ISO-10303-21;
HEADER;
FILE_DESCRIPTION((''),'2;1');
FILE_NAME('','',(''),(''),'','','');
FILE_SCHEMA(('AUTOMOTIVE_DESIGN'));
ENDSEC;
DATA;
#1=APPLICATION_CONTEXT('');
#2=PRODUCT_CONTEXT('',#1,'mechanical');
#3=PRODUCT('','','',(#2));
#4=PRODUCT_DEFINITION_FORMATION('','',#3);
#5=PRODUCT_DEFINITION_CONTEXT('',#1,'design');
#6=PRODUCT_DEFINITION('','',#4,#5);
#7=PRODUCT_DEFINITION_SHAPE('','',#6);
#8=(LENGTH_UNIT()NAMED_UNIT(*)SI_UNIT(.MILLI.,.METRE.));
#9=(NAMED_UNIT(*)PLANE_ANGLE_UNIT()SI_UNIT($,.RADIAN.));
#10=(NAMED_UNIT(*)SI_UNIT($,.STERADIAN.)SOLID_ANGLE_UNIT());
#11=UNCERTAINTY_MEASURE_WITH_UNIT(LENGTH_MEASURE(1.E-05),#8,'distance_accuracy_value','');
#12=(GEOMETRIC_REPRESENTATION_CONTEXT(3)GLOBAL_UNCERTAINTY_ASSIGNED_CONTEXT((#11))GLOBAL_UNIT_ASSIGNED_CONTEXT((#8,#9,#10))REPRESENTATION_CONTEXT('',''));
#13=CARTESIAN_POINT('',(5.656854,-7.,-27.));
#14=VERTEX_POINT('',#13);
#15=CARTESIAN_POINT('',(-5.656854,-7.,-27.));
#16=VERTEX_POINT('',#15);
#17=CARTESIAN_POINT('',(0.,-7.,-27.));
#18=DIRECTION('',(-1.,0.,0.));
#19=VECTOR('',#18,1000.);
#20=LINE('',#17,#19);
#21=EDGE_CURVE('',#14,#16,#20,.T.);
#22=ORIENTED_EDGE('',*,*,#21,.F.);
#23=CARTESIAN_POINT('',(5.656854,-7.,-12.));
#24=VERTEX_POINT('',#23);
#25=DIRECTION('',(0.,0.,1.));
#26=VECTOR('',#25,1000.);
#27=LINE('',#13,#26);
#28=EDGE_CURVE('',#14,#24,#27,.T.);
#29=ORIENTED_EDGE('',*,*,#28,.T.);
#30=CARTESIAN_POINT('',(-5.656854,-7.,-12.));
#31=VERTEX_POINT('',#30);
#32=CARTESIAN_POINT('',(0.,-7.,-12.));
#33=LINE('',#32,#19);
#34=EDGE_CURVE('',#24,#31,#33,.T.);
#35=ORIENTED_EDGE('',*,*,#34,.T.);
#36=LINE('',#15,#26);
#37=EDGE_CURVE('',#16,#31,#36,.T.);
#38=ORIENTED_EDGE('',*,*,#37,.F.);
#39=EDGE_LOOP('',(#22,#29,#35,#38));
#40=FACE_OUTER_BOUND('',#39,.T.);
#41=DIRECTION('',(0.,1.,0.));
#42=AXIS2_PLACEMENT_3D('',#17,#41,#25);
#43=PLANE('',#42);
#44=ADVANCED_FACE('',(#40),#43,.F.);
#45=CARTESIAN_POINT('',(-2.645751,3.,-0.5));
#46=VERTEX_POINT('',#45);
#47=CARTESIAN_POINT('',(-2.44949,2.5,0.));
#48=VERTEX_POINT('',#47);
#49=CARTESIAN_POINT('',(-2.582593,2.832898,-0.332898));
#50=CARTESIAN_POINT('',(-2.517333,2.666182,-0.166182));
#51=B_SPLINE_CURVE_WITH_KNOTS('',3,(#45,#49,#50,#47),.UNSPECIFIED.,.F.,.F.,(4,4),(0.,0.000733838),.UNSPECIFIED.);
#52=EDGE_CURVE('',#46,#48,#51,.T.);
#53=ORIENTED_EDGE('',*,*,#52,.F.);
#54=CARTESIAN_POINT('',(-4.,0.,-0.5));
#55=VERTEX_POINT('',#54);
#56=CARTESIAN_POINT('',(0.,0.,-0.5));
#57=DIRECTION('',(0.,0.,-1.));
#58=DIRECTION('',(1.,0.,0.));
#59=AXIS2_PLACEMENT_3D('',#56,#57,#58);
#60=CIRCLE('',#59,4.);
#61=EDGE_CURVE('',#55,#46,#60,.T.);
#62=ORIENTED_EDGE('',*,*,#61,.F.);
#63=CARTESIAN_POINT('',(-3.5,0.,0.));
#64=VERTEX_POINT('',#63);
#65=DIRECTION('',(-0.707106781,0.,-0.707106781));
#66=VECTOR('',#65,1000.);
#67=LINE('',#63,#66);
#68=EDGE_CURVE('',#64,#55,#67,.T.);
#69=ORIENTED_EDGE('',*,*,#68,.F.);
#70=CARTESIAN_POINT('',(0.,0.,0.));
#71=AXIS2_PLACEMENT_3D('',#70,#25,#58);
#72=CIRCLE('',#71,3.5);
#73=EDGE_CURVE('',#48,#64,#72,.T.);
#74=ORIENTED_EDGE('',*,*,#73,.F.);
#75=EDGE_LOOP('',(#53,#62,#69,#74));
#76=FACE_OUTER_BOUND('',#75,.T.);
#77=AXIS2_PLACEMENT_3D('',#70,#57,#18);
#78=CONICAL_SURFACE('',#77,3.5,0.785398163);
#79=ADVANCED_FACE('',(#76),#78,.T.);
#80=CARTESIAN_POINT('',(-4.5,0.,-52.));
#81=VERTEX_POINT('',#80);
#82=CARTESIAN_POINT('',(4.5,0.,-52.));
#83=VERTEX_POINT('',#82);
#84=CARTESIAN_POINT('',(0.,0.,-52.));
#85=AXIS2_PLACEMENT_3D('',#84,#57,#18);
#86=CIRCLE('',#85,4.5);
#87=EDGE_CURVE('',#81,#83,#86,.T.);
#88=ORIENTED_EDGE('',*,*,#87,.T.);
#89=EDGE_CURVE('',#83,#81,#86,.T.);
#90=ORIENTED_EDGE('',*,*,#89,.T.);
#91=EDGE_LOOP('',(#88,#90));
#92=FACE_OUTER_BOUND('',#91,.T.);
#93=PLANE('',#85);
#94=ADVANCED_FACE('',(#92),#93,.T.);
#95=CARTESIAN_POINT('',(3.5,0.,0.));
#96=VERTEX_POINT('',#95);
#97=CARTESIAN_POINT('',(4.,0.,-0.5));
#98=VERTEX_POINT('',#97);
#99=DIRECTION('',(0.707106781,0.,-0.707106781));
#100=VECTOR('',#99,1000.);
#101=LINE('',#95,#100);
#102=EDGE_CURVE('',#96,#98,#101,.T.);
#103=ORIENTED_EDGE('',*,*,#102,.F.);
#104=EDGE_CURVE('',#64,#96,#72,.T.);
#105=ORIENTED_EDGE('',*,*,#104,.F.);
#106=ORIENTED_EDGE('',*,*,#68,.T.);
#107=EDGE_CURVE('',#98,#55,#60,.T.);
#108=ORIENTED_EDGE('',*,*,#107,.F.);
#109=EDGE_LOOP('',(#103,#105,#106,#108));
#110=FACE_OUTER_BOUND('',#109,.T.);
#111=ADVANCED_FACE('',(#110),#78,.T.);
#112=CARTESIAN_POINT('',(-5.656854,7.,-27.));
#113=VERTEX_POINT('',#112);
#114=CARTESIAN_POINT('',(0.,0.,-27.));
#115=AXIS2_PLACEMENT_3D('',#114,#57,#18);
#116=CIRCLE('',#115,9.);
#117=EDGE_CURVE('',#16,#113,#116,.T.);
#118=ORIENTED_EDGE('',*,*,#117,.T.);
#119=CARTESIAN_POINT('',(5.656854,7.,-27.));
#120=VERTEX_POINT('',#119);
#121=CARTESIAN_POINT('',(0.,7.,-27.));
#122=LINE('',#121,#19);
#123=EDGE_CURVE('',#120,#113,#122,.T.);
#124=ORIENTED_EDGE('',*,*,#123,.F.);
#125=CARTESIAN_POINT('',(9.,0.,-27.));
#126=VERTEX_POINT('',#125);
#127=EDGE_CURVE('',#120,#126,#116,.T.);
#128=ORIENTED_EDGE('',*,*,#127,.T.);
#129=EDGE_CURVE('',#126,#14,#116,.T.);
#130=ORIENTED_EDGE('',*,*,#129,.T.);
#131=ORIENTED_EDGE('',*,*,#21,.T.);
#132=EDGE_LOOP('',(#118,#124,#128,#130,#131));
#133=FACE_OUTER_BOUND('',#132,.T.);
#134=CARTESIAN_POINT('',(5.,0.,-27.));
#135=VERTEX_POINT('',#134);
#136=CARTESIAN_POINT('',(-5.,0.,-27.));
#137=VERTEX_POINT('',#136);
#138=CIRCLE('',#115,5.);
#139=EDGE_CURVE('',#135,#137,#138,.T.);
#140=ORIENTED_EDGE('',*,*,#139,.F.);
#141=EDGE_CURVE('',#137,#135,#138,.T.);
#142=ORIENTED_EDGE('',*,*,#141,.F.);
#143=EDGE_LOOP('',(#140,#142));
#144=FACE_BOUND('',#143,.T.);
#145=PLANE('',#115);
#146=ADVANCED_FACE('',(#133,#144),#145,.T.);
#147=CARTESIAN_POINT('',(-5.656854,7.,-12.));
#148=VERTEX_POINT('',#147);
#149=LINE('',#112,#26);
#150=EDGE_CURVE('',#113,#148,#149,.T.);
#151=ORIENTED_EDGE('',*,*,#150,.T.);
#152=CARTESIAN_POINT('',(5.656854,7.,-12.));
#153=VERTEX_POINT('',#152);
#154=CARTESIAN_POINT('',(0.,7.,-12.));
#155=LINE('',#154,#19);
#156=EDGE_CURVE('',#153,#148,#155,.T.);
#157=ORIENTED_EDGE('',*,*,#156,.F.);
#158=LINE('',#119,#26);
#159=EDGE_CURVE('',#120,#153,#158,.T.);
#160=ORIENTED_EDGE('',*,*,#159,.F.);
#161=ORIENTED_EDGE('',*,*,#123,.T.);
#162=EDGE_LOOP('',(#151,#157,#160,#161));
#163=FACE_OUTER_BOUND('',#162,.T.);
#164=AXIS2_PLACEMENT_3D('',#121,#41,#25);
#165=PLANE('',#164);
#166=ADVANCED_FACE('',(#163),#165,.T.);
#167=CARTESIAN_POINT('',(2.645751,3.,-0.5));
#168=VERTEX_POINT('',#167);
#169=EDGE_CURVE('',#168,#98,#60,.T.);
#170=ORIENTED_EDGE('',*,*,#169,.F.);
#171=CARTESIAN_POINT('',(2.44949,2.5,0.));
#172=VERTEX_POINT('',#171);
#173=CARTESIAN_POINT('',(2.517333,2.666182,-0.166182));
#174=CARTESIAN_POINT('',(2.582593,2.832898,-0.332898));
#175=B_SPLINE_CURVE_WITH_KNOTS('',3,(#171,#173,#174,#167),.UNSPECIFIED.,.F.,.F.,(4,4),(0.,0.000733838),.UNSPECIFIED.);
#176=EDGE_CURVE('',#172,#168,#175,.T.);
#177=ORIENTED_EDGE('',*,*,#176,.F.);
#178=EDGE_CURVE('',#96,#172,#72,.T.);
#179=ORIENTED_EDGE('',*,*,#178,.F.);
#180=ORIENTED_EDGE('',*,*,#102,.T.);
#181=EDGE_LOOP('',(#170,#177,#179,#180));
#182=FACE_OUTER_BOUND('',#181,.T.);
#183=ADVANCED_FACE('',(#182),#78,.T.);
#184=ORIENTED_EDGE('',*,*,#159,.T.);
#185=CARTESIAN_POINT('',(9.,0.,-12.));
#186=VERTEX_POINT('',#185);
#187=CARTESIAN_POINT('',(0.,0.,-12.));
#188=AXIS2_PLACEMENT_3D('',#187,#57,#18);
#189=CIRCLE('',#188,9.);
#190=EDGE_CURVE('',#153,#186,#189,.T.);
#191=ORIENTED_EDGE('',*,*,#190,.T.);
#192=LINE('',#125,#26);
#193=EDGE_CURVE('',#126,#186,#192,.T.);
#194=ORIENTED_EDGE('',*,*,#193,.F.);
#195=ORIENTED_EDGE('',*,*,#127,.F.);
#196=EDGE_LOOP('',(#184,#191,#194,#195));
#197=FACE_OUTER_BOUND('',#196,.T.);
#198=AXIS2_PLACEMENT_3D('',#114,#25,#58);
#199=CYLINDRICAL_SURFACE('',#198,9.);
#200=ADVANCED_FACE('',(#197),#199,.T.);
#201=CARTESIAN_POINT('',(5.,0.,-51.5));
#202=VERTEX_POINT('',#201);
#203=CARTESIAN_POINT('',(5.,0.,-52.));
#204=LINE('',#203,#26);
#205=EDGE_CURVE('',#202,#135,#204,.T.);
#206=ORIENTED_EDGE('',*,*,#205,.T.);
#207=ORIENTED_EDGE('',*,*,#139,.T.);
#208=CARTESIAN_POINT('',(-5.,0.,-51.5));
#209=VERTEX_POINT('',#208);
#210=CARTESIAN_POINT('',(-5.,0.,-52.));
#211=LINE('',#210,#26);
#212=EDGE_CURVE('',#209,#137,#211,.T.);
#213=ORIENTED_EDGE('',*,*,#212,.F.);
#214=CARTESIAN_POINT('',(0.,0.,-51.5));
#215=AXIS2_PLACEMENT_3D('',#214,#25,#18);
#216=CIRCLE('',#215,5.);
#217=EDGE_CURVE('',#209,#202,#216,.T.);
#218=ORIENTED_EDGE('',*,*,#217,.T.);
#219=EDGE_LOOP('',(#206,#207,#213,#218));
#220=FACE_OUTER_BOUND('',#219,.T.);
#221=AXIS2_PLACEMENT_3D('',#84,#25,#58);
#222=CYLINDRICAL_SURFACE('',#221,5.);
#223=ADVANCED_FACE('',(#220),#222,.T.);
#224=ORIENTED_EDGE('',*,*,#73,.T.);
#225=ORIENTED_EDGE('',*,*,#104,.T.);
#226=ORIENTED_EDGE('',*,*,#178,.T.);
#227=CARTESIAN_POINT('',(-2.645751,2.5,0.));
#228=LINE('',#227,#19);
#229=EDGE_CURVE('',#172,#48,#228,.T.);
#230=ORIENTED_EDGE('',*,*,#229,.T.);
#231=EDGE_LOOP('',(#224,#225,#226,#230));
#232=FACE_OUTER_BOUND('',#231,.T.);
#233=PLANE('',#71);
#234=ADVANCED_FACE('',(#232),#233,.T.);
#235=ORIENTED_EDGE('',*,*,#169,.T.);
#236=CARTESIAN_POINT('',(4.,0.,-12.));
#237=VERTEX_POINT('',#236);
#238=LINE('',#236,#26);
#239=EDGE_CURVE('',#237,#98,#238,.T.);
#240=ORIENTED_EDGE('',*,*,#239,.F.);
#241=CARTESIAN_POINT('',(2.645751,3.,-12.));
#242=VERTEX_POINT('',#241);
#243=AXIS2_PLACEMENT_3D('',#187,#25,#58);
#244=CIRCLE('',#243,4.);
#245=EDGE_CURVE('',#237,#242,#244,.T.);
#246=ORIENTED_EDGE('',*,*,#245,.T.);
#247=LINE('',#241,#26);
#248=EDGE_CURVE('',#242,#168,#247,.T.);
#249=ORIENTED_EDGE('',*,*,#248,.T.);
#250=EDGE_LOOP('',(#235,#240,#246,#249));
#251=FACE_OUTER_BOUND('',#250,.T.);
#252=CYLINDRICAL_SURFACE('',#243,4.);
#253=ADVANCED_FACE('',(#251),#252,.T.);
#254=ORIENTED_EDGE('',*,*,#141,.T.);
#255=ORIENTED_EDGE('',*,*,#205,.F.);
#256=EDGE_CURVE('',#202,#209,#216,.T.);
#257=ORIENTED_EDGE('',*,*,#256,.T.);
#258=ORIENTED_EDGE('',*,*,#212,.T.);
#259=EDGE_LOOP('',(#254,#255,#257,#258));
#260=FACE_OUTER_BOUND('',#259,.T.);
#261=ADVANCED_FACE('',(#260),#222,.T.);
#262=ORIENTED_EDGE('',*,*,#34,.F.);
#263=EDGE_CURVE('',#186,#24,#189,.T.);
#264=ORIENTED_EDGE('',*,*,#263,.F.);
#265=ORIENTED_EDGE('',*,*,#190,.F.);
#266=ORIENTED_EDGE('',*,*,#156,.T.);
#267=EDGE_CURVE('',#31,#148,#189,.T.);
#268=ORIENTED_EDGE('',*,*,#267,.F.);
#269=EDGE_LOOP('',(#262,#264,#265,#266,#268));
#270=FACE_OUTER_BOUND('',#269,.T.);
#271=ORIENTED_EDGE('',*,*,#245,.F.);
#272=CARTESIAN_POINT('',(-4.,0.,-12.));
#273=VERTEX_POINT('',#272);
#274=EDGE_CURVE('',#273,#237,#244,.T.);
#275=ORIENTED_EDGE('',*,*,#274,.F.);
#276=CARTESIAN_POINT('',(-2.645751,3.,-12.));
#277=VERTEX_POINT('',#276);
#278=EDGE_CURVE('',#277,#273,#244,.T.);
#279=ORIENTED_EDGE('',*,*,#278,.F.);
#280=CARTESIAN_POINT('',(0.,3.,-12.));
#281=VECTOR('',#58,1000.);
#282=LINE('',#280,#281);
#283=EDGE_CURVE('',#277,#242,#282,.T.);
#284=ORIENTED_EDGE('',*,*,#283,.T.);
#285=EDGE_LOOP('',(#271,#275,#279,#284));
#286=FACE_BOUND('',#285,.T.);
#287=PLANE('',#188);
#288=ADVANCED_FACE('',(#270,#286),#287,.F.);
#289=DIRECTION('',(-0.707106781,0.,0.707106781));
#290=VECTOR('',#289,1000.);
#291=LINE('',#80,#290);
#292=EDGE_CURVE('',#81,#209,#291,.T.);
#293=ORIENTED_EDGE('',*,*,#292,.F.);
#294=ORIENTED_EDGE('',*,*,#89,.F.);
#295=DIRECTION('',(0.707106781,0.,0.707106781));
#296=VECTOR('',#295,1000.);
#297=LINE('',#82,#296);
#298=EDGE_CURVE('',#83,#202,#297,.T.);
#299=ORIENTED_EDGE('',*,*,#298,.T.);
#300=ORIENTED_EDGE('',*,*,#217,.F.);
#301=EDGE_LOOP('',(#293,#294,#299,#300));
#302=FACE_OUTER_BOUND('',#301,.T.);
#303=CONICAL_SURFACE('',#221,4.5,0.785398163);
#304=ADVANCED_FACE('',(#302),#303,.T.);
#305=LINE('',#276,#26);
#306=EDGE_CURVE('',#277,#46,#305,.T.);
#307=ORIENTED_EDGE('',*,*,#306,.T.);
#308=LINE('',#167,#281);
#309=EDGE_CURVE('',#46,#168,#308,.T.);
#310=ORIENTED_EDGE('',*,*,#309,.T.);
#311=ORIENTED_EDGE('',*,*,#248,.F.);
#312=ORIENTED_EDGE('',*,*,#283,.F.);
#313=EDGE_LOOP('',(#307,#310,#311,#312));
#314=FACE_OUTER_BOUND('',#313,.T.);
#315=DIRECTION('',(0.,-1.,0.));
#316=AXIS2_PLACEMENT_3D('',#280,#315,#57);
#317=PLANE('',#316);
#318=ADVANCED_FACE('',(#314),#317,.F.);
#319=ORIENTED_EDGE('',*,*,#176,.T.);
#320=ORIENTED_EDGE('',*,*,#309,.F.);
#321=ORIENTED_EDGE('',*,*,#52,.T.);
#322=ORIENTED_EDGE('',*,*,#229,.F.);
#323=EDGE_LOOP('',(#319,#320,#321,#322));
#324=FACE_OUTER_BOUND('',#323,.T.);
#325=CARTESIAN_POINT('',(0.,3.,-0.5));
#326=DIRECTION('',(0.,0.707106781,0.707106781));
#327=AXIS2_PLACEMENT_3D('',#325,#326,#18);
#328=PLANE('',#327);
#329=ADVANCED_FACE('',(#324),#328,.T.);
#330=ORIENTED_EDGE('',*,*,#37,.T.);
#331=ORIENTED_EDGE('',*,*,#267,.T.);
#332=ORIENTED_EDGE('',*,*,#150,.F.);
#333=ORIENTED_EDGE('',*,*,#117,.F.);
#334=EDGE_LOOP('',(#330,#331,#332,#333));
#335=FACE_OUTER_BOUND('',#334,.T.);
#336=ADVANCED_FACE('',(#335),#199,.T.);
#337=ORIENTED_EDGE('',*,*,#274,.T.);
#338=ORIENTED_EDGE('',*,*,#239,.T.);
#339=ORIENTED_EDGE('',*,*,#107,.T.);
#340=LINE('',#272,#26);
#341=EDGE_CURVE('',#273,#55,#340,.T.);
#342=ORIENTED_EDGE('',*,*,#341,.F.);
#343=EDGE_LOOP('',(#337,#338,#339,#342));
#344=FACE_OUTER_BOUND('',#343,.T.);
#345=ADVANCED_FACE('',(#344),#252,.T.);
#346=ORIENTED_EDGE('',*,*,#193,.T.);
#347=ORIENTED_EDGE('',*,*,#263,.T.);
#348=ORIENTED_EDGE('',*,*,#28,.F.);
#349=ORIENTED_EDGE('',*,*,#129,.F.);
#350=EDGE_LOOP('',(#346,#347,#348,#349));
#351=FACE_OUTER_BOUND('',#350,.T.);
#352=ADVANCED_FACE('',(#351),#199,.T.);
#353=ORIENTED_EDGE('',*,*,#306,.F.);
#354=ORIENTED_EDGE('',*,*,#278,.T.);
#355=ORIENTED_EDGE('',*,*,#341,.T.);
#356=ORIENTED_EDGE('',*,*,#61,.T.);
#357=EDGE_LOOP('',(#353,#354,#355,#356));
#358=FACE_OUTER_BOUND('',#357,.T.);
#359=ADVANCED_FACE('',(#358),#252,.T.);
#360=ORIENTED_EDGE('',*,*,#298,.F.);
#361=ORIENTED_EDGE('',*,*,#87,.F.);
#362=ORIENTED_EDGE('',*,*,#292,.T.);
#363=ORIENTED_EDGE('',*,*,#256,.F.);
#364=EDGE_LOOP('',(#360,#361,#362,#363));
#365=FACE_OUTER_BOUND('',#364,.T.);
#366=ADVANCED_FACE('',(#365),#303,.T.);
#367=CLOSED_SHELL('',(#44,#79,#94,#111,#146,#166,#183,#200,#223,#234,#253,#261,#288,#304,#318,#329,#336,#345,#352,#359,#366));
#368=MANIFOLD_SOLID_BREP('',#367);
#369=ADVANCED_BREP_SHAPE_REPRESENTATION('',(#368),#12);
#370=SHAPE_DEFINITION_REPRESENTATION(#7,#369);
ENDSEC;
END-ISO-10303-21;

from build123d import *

# Parameters (mm, degrees)
BOSS_EXTRUDE1_DEPTH = 12
BOSS_EXTRUDE2_DEPTH = 15
SKETCH3_R           = 5
BOSS_EXTRUDE3_DEPTH = 25
CHAMFER1_SIZE       = 0.5


with BuildPart() as part:
    # Sketch1 → Boss-Extrude1 (new body)
    with BuildSketch(Plane.XY):
        with BuildLine():
            Line((2.645751311, 3), (-2.645751311, 3))
            ThreePointArc((-2.645751311, 3), (-1.645751311, -3.645751311), (4, 0))
            ThreePointArc((4, 0), (3.645751311, 1.645751311), (2.645751311, 3))
        make_face()
    extrude(amount=-BOSS_EXTRUDE1_DEPTH)

    # Sketch2 → Boss-Extrude2 (add)
    # profile 1 of 2: a face of its own
    with BuildSketch(Plane(origin=(0, 0, -12), x_dir=(-1, 0, 0), z_dir=(0, 0, -1))):
        with BuildLine():
            Line((5.656854249, 7), (-5.656854249, 7))
            ThreePointArc((-5.656854249, 7), (-9, 0), (-5.656854249, -7))
            Line((-5.656854249, -7), (5.656854249, -7))
            ThreePointArc((5.656854249, -7), (8.121320344, -3.878679656), (9, 0))
            ThreePointArc((9, 0), (8.121320344, 3.878679656), (5.656854249, 7))
        make_face()
        with BuildLine():
            ThreePointArc((2.645751311, 3), (0, -4), (-2.645751311, 3))
            Line((-2.645751311, 3), (2.645751311, 3))
        make_face(mode=Mode.SUBTRACT)
    # profile 2 of 2: a face of its own
    with BuildSketch(Plane(origin=(0, 0, -12), x_dir=(-1, 0, 0), z_dir=(0, 0, -1))):
        with BuildLine():
            Line((2.645751311, 3), (-2.645751311, 3))
            ThreePointArc((-2.645751311, 3), (0, -4), (2.645751311, 3))
        make_face()
    extrude(amount=BOSS_EXTRUDE2_DEPTH)

    # Sketch3 → Boss-Extrude3 (add)
    with BuildSketch(Plane(origin=(0, 0, -27), x_dir=(-1, 0, 0), z_dir=(0, 0, -1))):
        Circle(SKETCH3_R)
    extrude(amount=BOSS_EXTRUDE3_DEPTH)

    # Chamfer1
    chamfer1_edges = [part.edges().sort_by_distance(p)[0] for p in [
        (5, 0, -52),
        (0, 3, 0),
        (0, -4, 0),
    ]]
    chamfer(chamfer1_edges, length=CHAMFER1_SIZE)


solid = part.part
